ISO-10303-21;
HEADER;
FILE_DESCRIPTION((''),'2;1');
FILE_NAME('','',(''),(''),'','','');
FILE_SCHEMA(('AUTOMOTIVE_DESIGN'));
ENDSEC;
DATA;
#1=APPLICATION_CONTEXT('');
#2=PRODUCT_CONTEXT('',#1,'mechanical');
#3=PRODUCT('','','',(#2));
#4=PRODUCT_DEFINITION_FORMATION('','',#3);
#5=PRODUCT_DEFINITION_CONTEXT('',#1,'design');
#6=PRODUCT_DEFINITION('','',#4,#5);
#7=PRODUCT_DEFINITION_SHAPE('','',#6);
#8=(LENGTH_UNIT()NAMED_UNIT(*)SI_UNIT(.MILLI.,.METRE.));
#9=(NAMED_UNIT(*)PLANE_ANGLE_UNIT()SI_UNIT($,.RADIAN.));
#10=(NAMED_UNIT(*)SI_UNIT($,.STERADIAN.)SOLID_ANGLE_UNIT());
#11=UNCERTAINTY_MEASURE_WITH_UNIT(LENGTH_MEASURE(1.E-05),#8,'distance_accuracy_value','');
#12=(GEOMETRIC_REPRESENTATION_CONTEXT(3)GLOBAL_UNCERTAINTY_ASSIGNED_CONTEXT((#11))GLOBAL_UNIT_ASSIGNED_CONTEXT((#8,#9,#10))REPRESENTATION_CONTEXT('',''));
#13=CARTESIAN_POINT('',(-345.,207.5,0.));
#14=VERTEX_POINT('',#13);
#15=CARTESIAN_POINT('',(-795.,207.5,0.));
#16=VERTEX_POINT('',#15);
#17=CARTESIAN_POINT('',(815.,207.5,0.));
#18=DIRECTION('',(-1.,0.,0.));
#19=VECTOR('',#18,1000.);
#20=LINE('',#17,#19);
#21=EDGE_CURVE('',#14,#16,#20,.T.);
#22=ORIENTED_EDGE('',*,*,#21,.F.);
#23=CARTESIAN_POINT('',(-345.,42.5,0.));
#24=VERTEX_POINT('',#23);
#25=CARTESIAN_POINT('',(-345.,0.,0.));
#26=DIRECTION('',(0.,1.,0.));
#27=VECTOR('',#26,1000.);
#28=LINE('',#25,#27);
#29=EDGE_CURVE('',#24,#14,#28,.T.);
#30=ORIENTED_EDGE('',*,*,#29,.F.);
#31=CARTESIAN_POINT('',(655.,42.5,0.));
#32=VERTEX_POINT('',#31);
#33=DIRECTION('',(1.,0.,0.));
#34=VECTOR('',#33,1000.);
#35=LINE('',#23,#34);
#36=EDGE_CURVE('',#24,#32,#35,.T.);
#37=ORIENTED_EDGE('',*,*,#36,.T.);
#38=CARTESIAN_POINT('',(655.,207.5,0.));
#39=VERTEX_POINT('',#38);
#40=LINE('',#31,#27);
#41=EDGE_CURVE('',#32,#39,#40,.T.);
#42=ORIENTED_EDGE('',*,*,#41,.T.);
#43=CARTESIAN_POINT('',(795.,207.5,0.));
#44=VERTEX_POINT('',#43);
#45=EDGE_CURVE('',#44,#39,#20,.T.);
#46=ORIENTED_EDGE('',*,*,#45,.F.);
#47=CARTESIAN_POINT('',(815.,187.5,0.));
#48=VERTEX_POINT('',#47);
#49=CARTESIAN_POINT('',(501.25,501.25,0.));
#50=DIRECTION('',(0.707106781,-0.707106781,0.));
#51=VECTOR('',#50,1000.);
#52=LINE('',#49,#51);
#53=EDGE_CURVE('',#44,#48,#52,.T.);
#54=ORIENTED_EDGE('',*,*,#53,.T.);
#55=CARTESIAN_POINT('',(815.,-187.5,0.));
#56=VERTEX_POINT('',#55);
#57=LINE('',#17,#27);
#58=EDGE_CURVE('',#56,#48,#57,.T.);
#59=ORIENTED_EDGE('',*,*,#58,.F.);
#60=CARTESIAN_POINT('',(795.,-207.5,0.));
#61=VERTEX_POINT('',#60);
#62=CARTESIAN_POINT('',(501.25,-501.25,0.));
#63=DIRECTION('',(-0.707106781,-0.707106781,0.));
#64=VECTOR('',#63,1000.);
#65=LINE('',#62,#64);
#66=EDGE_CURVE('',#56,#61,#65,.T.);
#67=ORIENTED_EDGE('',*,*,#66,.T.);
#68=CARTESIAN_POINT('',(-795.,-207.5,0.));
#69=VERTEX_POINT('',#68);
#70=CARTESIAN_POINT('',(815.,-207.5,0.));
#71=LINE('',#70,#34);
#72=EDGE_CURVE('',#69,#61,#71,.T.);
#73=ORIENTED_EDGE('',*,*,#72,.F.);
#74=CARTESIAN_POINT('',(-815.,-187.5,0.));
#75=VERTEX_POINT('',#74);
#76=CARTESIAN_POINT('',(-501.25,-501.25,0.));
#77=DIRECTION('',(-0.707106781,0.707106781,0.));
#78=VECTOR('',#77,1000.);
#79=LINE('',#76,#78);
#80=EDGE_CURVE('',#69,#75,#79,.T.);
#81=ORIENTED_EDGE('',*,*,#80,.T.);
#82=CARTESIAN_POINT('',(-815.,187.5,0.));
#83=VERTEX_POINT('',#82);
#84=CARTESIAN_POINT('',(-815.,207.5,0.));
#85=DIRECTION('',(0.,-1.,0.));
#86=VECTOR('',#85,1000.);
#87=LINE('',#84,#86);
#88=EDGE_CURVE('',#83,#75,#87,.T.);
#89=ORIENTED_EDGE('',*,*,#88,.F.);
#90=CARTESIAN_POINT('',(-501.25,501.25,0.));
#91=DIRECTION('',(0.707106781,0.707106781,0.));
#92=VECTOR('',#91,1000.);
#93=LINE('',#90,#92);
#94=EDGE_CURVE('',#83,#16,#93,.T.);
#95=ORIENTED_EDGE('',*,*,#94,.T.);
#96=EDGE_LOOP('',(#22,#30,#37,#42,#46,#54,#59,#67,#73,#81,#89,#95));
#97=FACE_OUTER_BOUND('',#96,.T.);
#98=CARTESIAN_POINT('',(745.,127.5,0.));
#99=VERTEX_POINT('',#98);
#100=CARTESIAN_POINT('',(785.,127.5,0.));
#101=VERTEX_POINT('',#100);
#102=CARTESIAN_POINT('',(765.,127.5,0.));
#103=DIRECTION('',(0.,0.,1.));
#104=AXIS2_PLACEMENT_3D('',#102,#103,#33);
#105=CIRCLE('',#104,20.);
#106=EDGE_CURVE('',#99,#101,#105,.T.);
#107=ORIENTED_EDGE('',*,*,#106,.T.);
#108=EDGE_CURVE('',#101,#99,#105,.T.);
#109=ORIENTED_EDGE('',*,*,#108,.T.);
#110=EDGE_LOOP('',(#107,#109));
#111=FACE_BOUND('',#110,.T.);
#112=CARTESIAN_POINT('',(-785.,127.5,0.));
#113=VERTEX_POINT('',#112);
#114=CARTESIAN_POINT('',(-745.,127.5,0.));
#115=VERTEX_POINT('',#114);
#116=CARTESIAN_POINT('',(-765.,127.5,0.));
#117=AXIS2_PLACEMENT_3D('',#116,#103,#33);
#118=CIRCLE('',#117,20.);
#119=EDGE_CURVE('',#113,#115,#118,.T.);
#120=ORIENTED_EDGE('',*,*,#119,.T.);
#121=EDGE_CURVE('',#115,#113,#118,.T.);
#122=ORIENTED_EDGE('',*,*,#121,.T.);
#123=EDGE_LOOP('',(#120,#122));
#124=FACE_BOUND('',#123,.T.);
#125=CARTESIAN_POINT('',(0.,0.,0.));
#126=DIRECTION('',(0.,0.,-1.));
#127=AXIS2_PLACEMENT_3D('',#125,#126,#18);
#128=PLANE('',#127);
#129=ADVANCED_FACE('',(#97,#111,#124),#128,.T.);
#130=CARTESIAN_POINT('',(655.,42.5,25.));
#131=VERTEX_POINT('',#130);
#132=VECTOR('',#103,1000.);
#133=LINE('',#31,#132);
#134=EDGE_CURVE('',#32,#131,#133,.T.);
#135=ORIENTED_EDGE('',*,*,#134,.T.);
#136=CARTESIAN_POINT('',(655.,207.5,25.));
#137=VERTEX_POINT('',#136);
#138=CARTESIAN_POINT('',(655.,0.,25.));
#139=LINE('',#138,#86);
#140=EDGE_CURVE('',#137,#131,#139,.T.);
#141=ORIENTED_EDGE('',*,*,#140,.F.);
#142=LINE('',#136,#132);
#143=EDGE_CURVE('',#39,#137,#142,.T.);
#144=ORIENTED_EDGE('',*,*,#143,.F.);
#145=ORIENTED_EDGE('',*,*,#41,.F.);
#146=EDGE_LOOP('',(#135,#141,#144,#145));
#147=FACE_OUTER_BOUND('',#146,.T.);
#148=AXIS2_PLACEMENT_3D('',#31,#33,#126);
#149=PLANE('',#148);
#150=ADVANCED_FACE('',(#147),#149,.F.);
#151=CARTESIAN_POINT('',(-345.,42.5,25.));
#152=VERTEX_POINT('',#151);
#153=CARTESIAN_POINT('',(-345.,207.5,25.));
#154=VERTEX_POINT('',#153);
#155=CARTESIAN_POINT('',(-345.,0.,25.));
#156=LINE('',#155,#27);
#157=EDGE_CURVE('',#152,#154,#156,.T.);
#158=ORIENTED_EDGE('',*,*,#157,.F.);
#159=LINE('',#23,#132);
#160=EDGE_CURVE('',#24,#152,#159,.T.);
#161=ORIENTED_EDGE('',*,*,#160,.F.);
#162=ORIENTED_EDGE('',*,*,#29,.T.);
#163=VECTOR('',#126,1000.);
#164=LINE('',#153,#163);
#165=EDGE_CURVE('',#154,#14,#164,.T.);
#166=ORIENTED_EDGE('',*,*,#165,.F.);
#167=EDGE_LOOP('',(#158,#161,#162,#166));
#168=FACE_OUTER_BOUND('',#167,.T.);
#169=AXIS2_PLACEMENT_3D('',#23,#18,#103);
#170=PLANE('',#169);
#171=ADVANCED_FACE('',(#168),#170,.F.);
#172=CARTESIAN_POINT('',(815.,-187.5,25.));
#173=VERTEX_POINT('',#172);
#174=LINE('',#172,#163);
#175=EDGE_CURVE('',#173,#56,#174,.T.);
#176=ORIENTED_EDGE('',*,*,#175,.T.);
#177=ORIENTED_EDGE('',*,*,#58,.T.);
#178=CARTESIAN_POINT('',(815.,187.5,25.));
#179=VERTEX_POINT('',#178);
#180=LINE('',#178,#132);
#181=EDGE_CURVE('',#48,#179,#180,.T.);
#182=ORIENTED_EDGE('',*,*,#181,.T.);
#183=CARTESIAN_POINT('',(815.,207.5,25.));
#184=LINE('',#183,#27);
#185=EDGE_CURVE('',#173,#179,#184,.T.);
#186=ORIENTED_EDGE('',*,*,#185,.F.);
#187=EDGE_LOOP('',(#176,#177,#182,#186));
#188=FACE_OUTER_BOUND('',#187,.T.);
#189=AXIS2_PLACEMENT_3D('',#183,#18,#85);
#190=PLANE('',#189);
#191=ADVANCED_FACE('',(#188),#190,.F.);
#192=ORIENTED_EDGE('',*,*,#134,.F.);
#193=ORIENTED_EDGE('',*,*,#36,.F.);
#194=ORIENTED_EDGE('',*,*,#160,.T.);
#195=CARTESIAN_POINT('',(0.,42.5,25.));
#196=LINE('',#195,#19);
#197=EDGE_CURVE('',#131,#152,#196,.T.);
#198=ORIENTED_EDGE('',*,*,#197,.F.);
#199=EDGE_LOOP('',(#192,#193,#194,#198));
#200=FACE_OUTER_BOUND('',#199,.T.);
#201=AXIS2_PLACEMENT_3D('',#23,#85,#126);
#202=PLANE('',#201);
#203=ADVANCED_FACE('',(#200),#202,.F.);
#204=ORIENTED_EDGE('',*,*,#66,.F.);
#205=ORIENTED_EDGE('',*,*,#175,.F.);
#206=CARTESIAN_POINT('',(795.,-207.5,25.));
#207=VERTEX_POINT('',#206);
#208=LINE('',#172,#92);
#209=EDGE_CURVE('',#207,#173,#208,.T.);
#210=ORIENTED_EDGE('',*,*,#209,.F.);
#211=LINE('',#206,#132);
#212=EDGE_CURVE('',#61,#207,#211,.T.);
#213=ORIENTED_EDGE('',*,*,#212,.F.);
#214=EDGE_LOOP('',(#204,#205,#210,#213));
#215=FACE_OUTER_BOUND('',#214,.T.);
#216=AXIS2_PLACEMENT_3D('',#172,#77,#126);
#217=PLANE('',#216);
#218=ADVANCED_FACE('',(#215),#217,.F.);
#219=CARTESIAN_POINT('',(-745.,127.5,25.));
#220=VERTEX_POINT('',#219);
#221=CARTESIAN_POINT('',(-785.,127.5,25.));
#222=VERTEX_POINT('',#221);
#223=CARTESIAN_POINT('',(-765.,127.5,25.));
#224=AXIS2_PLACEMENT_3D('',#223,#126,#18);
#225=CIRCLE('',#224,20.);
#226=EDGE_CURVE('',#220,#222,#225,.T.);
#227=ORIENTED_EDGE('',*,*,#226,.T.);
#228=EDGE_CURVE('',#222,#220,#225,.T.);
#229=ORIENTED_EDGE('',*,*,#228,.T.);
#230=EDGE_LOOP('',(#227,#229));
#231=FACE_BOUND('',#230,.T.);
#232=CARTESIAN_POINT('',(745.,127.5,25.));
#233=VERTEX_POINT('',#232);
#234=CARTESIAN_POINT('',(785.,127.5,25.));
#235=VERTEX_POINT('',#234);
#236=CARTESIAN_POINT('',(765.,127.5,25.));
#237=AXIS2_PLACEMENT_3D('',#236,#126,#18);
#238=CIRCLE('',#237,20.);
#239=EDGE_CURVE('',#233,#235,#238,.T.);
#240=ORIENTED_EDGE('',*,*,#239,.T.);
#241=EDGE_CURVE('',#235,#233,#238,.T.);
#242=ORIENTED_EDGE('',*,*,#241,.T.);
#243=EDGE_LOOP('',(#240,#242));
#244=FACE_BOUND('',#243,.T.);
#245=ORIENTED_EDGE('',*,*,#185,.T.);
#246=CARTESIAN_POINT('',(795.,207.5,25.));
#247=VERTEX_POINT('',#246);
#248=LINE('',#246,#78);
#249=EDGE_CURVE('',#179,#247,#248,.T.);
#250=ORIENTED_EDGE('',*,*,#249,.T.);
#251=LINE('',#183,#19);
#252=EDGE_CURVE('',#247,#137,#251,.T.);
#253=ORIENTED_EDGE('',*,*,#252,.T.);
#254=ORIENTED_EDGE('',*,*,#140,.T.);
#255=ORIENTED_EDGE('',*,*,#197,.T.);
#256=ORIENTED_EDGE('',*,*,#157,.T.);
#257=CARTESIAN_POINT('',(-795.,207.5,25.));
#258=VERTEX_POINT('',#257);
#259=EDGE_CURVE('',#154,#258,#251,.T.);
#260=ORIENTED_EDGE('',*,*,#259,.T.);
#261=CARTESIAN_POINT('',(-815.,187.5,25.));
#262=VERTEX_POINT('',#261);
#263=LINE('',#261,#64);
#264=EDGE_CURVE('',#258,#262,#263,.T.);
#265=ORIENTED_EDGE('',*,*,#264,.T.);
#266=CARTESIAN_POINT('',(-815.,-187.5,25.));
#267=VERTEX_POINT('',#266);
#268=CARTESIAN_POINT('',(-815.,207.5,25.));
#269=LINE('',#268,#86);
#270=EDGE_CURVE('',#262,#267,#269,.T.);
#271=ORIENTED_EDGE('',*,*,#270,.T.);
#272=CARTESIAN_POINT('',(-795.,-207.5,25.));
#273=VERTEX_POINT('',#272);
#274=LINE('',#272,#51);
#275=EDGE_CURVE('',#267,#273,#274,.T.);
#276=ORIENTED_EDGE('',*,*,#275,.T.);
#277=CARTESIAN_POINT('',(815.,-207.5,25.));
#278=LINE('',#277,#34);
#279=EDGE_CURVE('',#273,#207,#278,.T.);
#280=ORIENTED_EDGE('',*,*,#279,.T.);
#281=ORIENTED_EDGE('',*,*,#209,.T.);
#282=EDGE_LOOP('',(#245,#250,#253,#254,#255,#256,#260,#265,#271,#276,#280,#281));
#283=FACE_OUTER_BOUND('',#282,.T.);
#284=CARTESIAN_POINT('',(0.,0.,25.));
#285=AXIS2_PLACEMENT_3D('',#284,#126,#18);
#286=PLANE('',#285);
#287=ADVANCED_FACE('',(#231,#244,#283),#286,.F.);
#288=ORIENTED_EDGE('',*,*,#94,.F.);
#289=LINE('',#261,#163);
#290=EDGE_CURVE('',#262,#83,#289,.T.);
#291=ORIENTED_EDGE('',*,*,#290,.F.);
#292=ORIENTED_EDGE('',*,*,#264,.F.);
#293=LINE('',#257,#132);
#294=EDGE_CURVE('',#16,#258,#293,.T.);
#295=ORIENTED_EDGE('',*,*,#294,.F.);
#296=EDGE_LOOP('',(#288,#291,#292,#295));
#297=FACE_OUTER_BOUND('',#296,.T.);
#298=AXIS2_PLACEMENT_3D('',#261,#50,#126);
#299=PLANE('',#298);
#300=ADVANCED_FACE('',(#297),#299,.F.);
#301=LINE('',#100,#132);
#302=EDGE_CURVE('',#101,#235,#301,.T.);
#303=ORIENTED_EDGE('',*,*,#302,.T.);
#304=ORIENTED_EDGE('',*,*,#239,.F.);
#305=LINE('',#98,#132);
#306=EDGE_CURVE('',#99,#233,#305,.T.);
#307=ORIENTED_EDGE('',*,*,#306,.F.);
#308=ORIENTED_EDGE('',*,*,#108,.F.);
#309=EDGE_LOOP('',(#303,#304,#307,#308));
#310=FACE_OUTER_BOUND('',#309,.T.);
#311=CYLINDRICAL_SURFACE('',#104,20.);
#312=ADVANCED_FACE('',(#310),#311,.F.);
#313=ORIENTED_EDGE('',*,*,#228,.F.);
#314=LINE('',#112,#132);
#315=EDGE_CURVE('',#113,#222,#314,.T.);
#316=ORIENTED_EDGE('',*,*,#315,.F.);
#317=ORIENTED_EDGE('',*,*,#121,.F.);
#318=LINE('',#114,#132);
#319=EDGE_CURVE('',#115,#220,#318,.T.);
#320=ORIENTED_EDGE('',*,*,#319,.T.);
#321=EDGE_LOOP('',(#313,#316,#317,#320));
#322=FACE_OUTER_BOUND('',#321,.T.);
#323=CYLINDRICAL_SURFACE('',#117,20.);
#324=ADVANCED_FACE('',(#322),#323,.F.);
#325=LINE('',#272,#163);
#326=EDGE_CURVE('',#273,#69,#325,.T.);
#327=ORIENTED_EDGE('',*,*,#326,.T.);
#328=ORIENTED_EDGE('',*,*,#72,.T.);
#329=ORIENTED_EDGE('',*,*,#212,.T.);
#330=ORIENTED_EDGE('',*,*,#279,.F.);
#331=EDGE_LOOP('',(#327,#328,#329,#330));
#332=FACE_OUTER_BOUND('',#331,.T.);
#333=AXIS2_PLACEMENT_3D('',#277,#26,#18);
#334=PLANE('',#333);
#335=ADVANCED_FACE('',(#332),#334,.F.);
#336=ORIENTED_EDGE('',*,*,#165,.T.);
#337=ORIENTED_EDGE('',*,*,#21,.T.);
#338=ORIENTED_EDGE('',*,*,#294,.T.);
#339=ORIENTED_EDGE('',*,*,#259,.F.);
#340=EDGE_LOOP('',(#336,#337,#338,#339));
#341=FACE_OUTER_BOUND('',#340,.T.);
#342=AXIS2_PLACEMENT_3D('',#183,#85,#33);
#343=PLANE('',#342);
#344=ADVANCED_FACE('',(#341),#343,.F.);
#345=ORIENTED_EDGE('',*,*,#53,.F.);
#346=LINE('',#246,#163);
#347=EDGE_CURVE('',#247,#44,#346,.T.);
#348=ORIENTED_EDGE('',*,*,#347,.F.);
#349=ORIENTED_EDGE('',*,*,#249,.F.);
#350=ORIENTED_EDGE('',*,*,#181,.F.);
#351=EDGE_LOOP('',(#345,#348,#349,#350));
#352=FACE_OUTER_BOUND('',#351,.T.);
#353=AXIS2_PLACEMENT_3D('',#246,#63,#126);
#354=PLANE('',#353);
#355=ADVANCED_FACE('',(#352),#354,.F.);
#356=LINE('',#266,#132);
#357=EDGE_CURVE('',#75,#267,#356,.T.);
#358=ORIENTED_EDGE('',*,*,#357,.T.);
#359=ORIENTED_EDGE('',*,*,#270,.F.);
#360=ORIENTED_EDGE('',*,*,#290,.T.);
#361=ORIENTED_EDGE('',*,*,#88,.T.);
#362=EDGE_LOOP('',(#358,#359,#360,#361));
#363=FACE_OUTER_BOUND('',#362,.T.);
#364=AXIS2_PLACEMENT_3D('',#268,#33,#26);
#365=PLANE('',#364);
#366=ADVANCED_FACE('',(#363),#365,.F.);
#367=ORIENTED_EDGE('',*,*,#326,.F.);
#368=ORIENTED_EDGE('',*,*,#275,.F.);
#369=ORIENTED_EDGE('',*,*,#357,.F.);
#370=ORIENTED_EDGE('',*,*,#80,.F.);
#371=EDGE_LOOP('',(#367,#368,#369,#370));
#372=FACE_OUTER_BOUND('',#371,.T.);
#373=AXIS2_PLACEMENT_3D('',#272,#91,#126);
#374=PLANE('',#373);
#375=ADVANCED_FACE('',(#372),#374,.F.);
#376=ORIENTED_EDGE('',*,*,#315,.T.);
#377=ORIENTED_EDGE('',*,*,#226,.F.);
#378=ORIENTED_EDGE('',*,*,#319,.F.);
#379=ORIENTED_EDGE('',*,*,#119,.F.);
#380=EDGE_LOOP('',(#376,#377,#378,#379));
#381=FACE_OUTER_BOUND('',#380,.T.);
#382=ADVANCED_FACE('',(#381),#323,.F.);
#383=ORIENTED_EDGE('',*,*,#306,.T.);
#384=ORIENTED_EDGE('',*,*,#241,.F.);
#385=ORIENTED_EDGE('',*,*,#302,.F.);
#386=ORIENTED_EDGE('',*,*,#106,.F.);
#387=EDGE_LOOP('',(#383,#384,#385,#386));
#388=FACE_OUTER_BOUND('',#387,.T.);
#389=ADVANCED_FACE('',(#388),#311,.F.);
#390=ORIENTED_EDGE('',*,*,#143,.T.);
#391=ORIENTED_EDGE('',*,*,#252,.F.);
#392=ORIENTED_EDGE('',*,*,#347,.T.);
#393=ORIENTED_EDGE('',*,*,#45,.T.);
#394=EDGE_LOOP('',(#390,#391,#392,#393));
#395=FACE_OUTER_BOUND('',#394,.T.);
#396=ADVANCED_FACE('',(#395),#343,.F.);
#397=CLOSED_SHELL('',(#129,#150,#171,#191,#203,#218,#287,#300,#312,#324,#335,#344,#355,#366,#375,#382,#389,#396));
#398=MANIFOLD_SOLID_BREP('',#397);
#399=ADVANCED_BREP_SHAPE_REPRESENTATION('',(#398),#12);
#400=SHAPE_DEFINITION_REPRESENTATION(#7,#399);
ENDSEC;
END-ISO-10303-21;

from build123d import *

# Parameters (mm, degrees)
SKETCH1_W               = 1630
SKETCH1_H               = 415
BOSS_EXTRUDE1_DEPTH     = 25
CHAMFER1_SIZE           = 20
CUT_EXTRUDE1_DEPTH      = 842.371647965
CUT_EXTRUDE1_DEPTH_BACK = 842.371647965
SKETCH2_R               = 20
SKETCH2_W               = 1000
SKETCH2_H               = 200


with BuildPart() as part:
    # Sketch1 → Boss-Extrude1 (new body)
    with BuildSketch(Plane.XY):
        Rectangle(SKETCH1_W, SKETCH1_H)
    extrude(amount=BOSS_EXTRUDE1_DEPTH)

    # Chamfer1
    chamfer1_edges = [part.edges().sort_by_distance(p)[0] for p in [
        (-815, 207.5, 12.5),
        (815, 207.5, 12.5),
        (815, -207.5, 12.5),
        (-815, -207.5, 12.5),
    ]]
    chamfer(chamfer1_edges, length=CHAMFER1_SIZE)

    # Sketch2 → Cut-Extrude1 (cut, two sides: drawn at the far end of the back side and taken through both)
    with BuildSketch(Plane.XY.offset(25).offset(-CUT_EXTRUDE1_DEPTH_BACK)):
        with Locations((-765, 127.5)):
            Circle(SKETCH2_R)
        with Locations((765, 127.5)):
            Circle(SKETCH2_R)
        with Locations((155, 142.5)):
            Rectangle(SKETCH2_W, SKETCH2_H)
    extrude(amount=CUT_EXTRUDE1_DEPTH + CUT_EXTRUDE1_DEPTH_BACK, mode=Mode.SUBTRACT)


solid = part.part
